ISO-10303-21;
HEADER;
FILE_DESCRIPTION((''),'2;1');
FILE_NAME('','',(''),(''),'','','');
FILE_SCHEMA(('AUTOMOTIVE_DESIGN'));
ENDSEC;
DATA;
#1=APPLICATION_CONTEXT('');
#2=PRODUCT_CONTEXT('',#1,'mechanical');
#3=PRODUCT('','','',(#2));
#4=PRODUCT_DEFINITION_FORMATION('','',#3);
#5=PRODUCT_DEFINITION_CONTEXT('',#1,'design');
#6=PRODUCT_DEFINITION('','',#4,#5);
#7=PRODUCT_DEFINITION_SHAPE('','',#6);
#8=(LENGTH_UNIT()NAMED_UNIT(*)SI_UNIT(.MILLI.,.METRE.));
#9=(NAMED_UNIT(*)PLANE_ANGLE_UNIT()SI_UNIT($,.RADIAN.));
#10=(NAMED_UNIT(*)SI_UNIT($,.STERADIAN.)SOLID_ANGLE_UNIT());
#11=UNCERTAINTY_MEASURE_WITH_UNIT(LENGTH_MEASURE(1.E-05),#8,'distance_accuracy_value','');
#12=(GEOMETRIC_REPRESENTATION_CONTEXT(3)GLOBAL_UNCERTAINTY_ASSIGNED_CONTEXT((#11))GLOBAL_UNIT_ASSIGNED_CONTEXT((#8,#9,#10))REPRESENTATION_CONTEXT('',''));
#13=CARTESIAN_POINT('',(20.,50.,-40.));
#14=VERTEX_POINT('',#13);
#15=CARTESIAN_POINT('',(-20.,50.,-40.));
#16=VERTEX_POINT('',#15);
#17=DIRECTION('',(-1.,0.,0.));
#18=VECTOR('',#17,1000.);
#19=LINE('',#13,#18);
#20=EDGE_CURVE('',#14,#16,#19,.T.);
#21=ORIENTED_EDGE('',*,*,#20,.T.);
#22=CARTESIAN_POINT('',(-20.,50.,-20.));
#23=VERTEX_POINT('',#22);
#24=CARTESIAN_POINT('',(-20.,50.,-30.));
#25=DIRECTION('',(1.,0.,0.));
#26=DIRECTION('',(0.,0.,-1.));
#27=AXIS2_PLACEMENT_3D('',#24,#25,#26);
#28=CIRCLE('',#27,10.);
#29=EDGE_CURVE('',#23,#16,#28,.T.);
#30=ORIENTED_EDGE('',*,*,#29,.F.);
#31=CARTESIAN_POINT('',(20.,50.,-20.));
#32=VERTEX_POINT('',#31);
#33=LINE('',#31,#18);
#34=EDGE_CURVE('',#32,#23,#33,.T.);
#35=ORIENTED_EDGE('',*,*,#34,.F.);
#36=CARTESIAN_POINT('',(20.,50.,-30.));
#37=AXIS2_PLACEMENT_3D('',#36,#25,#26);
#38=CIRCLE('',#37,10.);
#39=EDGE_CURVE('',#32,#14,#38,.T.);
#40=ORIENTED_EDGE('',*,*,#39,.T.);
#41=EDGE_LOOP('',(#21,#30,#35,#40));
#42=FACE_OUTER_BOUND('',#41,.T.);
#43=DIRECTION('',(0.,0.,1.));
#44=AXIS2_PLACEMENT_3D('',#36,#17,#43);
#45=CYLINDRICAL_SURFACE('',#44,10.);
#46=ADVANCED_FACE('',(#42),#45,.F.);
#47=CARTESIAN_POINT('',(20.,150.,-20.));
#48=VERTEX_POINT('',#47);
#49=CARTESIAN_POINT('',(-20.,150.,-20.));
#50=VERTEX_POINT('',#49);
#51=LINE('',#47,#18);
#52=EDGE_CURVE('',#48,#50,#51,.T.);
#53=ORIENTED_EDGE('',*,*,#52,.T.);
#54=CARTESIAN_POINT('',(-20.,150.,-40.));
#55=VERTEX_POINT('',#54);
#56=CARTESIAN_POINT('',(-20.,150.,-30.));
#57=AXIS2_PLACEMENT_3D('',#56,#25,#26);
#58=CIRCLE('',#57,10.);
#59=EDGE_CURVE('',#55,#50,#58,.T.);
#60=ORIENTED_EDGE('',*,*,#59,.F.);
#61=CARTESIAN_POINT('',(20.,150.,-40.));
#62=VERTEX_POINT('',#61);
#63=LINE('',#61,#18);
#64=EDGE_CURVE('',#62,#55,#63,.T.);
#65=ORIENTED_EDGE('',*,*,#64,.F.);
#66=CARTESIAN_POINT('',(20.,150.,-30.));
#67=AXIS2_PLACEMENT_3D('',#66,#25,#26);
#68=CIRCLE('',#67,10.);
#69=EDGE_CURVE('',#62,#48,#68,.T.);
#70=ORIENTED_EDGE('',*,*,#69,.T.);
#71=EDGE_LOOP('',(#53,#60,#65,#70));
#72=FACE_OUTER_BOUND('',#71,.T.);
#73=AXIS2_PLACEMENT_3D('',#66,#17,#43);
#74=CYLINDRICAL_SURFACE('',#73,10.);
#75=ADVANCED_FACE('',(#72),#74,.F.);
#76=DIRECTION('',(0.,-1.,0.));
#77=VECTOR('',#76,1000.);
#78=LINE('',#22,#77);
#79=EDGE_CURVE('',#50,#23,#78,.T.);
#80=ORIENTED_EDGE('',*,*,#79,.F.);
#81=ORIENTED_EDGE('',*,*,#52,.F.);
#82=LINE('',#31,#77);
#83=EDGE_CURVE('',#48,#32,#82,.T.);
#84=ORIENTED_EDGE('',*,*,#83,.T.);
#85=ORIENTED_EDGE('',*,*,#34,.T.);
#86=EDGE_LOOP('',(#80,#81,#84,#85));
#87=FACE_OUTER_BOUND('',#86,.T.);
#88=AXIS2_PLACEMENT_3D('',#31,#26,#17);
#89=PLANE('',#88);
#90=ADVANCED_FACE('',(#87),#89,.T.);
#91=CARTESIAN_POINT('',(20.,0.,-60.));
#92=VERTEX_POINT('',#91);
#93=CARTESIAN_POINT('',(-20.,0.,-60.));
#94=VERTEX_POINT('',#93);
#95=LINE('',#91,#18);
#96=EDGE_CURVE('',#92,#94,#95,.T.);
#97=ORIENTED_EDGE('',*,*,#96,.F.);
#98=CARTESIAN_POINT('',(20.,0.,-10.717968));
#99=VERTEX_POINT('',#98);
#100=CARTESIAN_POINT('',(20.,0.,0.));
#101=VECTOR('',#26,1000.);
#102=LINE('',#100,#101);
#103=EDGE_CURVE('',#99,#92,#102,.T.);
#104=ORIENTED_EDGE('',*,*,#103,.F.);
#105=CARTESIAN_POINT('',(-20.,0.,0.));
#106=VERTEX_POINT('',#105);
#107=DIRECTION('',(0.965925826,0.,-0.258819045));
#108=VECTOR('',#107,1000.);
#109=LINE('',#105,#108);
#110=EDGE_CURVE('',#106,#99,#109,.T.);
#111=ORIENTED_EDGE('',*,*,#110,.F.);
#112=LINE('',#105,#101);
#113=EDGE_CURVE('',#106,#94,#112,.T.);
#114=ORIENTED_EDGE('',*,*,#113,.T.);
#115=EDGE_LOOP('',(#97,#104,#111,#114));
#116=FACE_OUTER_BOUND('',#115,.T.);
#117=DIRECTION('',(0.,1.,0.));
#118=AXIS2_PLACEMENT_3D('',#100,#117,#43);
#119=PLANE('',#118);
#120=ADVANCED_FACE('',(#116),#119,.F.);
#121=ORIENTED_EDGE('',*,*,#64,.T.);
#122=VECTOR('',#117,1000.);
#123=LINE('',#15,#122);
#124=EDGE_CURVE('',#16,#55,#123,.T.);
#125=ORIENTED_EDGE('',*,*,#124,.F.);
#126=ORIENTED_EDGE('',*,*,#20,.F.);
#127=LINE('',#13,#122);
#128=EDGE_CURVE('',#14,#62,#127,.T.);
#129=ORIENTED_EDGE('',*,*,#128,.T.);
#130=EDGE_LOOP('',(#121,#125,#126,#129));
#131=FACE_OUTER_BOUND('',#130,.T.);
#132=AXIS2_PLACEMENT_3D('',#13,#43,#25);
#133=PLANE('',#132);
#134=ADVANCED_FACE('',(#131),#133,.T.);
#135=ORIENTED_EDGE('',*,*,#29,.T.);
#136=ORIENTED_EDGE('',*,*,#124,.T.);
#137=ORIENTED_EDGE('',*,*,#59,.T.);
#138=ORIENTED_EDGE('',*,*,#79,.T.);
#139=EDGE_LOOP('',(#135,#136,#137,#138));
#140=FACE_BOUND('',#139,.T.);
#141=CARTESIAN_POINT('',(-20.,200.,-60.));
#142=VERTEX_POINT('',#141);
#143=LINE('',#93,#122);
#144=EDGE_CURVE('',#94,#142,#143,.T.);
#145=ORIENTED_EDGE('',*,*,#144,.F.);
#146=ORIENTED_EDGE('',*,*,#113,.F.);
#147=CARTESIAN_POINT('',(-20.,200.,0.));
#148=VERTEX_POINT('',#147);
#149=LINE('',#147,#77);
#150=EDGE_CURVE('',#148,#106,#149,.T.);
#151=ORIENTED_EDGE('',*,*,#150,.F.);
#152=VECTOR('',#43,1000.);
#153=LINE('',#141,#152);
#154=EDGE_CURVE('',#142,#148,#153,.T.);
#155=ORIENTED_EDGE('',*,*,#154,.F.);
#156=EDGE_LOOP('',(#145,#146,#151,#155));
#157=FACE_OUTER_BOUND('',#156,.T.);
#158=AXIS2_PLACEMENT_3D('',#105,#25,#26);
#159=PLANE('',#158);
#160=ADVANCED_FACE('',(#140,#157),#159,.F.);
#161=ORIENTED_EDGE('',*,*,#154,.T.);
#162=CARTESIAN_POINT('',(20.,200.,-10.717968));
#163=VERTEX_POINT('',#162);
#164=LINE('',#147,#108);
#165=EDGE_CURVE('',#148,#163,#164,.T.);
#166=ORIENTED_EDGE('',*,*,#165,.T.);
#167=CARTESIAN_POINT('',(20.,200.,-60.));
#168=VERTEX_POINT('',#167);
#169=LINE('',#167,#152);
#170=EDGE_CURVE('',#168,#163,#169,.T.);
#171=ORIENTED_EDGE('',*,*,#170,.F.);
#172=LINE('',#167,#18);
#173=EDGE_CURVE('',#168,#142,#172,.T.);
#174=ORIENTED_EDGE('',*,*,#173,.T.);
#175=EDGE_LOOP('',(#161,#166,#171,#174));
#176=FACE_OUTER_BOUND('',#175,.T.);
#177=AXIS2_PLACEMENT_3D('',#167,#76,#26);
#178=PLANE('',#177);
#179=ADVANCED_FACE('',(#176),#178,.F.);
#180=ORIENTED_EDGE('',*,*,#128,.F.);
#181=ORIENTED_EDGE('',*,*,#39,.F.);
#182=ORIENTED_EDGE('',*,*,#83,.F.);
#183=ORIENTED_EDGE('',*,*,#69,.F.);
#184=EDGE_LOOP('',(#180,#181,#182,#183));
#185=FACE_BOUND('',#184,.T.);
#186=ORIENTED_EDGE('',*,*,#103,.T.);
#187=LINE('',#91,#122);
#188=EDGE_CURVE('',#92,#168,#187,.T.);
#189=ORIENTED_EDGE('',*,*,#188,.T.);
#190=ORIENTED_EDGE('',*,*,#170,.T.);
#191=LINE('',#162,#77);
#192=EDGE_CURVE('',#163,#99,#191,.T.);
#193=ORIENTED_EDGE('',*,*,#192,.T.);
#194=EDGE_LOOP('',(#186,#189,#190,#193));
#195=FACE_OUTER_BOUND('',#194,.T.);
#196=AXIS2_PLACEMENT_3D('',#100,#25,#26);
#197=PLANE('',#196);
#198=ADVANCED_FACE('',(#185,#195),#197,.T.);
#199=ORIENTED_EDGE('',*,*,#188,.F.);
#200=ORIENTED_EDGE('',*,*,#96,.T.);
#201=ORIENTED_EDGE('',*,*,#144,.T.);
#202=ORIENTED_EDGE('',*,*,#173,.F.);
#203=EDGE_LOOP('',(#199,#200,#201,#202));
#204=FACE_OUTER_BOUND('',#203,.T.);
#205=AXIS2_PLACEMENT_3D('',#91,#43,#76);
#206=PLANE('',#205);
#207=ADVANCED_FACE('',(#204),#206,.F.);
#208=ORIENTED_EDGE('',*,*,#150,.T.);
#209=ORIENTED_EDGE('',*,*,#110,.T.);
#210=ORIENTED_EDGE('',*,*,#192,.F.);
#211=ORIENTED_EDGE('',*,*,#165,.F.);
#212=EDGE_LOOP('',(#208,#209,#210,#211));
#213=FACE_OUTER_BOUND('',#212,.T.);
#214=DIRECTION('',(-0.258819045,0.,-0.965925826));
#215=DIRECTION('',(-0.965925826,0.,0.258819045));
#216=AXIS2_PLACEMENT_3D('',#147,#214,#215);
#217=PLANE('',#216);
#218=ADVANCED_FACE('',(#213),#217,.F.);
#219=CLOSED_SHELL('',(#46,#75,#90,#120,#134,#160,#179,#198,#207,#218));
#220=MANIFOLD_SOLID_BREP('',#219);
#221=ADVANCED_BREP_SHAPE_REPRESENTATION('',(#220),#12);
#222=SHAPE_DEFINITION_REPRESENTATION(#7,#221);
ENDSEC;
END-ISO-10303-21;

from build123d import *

# Parameters (mm, degrees)
SKETCH1_W           = 60
SKETCH1_H           = 200
BOSS_EXTRUDE1_DEPTH = 20
CUT_EXTRUDE1_DEPTH  = 210.761769634


with BuildPart() as part:
    # Sketch1 → Boss-Extrude1 (new, symmetric)
    with BuildSketch(Plane(origin=(0, 0, 0), x_dir=(0, 0, -1), z_dir=(1, 0, 0))):
        with Locations((30, 100)):
            Rectangle(SKETCH1_W, SKETCH1_H)
        with BuildLine():
            Line((20, 50), (20, 150))
            ThreePointArc((20, 150), (30, 160), (40, 150))
            Line((40, 150), (40, 50))
            ThreePointArc((40, 50), (30, 40), (20, 50))
        make_face(mode=Mode.SUBTRACT)
    extrude(amount=BOSS_EXTRUDE1_DEPTH, both=True)

    # Sketch3 → Cut-Extrude1 (cut, through all)
    with BuildSketch(Plane.XZ):
        Polygon((-20, 0), (20, -10.717967697), (20, 0), align=None)
    extrude(amount=-CUT_EXTRUDE1_DEPTH, mode=Mode.SUBTRACT)


solid = part.part
